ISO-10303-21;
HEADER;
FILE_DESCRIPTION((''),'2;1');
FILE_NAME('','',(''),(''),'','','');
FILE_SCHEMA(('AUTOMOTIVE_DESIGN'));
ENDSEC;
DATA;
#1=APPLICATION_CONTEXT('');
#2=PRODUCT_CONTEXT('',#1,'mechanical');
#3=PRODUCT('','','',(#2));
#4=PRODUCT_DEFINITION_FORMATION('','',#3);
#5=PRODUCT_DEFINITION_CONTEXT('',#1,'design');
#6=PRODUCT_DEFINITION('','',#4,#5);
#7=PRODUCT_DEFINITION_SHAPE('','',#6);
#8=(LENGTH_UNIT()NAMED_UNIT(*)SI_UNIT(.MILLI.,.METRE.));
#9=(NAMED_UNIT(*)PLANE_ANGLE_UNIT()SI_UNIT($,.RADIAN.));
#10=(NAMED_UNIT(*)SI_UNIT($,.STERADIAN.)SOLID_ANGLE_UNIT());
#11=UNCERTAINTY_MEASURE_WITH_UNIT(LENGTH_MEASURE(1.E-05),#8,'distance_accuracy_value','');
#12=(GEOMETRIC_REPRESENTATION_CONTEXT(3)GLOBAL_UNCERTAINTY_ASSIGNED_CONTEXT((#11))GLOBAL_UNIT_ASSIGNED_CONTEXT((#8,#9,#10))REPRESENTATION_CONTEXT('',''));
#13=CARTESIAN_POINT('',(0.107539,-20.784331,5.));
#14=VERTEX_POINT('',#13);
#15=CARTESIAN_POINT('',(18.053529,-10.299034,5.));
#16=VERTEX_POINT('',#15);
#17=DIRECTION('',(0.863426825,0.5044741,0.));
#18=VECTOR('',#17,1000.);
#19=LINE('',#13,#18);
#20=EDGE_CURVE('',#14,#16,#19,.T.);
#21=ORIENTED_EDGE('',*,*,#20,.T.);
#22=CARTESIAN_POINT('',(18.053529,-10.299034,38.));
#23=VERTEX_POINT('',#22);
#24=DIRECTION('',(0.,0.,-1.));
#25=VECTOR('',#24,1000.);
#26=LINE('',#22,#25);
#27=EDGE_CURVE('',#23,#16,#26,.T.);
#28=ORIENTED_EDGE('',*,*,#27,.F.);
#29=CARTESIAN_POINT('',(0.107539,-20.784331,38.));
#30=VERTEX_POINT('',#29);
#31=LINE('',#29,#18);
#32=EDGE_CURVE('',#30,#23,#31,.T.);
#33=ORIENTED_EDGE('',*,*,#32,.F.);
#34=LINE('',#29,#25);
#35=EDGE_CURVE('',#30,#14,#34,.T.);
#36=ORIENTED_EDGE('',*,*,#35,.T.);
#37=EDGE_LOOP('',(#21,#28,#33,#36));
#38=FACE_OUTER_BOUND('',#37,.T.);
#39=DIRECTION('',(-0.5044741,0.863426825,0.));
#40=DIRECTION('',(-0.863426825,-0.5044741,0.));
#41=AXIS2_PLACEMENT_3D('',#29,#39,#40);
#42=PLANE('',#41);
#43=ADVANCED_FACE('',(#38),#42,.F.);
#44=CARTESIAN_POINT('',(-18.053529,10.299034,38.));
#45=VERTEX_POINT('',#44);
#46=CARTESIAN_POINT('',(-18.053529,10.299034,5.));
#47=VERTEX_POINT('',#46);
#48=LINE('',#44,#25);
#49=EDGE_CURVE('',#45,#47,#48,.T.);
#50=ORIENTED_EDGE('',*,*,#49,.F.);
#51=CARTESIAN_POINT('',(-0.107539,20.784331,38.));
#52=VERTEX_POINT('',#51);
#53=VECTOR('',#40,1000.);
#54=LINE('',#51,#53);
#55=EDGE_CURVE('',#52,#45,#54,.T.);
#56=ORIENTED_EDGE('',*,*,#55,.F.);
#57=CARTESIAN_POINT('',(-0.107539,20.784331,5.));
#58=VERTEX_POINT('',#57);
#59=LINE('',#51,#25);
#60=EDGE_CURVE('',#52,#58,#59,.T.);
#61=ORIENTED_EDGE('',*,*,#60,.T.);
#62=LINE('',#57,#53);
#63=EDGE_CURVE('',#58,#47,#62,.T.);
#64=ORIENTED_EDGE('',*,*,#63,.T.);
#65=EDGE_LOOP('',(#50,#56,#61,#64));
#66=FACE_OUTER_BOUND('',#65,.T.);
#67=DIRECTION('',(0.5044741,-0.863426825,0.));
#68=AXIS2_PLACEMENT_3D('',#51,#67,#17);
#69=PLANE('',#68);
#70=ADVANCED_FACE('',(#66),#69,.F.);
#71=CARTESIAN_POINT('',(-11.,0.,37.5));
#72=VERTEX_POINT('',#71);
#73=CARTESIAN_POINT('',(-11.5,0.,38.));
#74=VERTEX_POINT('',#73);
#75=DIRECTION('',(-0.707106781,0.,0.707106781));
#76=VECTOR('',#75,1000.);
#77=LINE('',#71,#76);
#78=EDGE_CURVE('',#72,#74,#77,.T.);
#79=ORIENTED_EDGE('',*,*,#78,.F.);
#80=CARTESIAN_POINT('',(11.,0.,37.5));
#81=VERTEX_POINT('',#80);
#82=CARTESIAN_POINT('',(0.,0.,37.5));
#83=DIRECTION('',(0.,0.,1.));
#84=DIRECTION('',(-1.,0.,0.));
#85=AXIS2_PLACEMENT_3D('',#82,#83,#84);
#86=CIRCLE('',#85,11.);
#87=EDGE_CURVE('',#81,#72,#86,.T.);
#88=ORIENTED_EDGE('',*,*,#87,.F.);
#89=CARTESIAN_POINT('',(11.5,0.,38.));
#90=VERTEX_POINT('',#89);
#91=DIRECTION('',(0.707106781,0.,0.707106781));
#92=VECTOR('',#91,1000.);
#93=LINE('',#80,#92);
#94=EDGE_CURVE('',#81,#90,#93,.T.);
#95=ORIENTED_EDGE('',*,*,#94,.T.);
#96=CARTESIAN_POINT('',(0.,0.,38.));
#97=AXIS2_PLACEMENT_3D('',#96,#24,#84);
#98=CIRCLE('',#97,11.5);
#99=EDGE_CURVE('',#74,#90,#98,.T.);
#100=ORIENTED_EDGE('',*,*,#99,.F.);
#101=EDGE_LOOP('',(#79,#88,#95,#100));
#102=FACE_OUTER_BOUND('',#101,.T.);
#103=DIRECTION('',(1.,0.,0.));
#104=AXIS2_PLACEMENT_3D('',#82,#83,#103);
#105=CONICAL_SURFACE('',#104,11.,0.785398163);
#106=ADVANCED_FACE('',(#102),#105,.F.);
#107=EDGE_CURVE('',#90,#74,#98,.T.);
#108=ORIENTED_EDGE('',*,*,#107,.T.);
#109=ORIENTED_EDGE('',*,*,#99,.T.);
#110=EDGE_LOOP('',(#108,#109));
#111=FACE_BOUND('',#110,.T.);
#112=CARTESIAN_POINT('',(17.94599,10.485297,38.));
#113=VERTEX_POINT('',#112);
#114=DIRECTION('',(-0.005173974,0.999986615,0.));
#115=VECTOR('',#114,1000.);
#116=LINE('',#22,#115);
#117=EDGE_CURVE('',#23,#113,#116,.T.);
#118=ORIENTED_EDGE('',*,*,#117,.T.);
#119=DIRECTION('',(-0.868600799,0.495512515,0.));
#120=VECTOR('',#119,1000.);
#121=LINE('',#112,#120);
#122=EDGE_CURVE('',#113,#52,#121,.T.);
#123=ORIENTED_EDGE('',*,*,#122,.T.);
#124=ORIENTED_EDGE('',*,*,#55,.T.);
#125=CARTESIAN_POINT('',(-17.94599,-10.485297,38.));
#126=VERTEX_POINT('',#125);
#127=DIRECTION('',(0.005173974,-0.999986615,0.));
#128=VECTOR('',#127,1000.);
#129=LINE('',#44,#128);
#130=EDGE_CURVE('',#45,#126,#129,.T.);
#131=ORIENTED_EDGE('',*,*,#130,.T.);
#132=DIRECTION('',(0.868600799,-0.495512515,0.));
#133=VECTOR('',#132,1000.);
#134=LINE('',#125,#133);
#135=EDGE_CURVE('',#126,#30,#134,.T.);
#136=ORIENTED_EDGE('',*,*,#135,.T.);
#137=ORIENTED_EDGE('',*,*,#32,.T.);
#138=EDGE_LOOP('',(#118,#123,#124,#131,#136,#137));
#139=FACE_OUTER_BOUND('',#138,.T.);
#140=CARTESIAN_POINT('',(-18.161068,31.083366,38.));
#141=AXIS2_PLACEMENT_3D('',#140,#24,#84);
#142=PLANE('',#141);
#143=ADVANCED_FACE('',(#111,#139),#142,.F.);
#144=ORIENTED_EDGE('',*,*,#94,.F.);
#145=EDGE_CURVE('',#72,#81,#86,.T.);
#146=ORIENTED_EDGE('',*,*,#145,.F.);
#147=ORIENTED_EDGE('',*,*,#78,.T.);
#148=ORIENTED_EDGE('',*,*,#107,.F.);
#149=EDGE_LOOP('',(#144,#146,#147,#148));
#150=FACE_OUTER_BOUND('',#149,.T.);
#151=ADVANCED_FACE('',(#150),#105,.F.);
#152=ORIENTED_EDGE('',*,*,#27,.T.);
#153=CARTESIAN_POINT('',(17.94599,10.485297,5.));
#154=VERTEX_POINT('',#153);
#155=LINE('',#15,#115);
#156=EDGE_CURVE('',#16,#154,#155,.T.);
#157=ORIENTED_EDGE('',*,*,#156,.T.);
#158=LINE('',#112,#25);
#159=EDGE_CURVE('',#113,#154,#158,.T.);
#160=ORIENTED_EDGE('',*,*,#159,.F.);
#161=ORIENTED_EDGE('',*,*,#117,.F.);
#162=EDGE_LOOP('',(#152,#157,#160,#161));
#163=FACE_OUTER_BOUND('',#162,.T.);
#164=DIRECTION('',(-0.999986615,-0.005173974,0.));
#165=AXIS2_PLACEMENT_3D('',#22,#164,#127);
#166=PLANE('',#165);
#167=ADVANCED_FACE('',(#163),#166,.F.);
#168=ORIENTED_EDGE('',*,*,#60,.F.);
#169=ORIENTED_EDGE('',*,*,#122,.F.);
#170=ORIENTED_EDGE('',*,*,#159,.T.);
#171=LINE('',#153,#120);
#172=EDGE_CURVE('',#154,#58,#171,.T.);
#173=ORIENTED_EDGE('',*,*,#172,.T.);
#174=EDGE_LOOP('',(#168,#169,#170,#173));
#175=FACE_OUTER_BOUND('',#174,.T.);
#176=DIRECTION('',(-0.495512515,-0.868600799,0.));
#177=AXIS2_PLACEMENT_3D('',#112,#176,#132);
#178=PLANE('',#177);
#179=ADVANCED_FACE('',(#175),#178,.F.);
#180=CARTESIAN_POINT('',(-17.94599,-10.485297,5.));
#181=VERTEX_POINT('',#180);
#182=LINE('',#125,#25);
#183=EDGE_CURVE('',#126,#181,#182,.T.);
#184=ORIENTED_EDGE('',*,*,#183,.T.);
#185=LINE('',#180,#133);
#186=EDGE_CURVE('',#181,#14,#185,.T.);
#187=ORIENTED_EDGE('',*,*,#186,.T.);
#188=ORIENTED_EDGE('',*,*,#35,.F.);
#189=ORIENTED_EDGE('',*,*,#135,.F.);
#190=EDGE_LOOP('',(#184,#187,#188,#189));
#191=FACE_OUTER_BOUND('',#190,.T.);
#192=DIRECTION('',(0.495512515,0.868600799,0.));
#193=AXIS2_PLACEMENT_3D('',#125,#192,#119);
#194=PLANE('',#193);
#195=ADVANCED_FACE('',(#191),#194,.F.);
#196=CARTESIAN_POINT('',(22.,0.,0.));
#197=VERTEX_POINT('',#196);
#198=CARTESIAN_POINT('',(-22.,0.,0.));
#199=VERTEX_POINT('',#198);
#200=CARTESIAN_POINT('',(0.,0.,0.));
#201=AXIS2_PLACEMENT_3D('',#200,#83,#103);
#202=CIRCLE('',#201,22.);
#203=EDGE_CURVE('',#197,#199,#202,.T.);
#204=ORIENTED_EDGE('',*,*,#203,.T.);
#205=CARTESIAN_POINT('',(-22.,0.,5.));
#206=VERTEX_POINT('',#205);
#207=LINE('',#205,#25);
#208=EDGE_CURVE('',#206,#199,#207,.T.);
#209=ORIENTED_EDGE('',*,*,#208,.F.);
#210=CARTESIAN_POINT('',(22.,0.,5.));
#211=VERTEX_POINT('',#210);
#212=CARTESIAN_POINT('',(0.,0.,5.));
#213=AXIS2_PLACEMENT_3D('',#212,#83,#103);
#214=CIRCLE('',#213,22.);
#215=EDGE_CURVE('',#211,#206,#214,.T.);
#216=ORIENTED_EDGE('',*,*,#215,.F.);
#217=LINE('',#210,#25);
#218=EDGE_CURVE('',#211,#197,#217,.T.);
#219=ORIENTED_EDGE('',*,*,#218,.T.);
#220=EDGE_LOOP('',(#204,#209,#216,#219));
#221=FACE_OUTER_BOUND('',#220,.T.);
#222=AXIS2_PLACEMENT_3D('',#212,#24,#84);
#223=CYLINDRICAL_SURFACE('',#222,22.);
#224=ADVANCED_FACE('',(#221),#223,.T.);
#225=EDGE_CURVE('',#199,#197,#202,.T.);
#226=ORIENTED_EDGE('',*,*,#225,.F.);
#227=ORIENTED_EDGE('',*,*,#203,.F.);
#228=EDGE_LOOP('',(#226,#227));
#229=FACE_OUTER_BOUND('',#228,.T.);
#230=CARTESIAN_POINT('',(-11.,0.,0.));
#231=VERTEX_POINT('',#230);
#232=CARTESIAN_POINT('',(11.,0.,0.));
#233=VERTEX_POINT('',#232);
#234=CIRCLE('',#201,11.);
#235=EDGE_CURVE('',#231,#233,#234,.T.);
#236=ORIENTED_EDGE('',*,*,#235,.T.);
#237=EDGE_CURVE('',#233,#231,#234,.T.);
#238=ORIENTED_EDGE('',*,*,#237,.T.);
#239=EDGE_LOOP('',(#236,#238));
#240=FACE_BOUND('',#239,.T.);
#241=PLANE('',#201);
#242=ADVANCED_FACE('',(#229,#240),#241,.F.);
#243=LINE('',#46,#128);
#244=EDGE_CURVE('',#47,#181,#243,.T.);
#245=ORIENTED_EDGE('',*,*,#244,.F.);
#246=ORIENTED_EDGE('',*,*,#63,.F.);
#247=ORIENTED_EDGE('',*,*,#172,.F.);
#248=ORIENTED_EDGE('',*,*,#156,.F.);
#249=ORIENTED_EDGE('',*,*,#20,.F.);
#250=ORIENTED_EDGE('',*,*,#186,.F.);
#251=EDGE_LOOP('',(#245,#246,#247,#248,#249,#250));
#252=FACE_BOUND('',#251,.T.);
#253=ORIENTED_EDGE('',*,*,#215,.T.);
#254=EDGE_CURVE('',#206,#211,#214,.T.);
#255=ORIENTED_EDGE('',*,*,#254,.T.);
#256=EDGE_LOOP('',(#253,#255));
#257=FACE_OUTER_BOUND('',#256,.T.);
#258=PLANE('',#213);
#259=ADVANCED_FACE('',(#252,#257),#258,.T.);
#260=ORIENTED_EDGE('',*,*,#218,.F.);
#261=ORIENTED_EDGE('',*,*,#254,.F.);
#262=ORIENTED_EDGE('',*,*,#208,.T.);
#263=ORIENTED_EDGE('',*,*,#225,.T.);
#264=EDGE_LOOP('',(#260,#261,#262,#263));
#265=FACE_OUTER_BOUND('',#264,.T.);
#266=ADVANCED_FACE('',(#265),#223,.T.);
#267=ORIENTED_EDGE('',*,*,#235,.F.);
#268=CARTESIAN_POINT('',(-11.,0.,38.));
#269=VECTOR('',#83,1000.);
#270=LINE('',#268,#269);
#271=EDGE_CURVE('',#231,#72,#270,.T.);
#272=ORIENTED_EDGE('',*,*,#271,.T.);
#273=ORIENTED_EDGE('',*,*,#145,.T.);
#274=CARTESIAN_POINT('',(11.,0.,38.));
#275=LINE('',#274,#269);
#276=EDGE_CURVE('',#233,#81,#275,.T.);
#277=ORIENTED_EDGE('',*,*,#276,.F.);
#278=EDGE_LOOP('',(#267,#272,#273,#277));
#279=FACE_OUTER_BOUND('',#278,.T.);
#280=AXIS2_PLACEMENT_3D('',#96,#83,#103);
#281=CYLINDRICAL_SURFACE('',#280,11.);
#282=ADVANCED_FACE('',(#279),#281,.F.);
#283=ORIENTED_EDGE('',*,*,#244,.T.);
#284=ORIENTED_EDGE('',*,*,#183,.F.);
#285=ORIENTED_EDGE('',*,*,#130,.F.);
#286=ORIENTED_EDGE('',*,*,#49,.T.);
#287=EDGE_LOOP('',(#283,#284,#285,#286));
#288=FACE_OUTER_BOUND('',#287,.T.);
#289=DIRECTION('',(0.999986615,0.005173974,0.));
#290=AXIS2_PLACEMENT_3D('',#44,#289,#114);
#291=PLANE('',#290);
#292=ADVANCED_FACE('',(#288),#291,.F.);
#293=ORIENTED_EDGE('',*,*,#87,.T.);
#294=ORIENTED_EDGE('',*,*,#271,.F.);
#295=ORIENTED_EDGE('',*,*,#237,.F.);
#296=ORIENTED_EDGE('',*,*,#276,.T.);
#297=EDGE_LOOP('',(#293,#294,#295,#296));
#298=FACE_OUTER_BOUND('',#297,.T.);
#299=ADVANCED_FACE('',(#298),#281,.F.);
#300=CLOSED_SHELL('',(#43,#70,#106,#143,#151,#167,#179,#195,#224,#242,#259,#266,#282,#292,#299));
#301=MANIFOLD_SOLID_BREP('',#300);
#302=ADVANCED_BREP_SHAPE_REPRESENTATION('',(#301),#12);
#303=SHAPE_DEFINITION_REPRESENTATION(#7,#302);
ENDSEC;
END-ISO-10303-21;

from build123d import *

# Parameters (mm, degrees)
SKETCH1_R                  = 22
BOSS_EXTRUDE_DEPTH         = 5
BOSS_EXTRUDE1_DEPTH        = 33
M24X2_0_TAPPED_HOLE1_D     = 22
M24X2_0_TAPPED_HOLE1_DEPTH = 58
M24X2_0_TAPPED_HOLE1_TIP   = 6.609466809
CHAMFER2_SIZE              = 0.5


with BuildPart() as part:
    # Sketch1 → Boss-Extrude (new body)
    with BuildSketch(Plane.XY):
        Circle(SKETCH1_R)
    extrude(amount=BOSS_EXTRUDE_DEPTH)

    # Sketch2 → Boss-Extrude1 (add)
    with BuildSketch(Plane.XY.offset(5)):
        Polygon((-17.945989557, -10.485297269), (0.107539023, -20.784331487), (18.05352858, -10.299034218), (17.945989557, 10.485297269), (-0.107539023, 20.784331487), (-18.05352858, 10.299034218), align=None)
    extrude(amount=BOSS_EXTRUDE1_DEPTH)

    # Sketch4 → Cut-Revolve1 (revolve, cut)
    with BuildSketch(Plane(origin=(0, 0, 0), x_dir=(0, 0, -1), z_dir=(1, 0, 0)), mode=Mode.PRIVATE) as cut_revolve1_sk:
        Polygon((-8.577004511, -2.997330388), (-6.875334866, -5.94470867), (-8.577004511, -5.94470867), align=None)
    revolve(cut_revolve1_sk.sketch.rotate(Axis((0, 0, 0), (0, 0, 1)), 270), axis=Axis((0, 0, 0), (0, 0, 1)), mode=Mode.SUBTRACT)

    # M24x2.0 Tapped Hole1
    with Locations(Plane.XY.offset(38)):
        with Locations((0, 0)):
            Hole(M24X2_0_TAPPED_HOLE1_D / 2, depth=M24X2_0_TAPPED_HOLE1_DEPTH)
            with Locations((0, 0, -(M24X2_0_TAPPED_HOLE1_DEPTH + M24X2_0_TAPPED_HOLE1_TIP / 2))):  # 118° drill point
                Cone(0, M24X2_0_TAPPED_HOLE1_D / 2, M24X2_0_TAPPED_HOLE1_TIP, mode=Mode.SUBTRACT)

    # Chamfer2
    chamfer2_edges = [part.edges().sort_by_distance(p)[0] for p in [
        (11, 0, 38),
    ]]
    chamfer(chamfer2_edges, length=CHAMFER2_SIZE)


solid = part.part
